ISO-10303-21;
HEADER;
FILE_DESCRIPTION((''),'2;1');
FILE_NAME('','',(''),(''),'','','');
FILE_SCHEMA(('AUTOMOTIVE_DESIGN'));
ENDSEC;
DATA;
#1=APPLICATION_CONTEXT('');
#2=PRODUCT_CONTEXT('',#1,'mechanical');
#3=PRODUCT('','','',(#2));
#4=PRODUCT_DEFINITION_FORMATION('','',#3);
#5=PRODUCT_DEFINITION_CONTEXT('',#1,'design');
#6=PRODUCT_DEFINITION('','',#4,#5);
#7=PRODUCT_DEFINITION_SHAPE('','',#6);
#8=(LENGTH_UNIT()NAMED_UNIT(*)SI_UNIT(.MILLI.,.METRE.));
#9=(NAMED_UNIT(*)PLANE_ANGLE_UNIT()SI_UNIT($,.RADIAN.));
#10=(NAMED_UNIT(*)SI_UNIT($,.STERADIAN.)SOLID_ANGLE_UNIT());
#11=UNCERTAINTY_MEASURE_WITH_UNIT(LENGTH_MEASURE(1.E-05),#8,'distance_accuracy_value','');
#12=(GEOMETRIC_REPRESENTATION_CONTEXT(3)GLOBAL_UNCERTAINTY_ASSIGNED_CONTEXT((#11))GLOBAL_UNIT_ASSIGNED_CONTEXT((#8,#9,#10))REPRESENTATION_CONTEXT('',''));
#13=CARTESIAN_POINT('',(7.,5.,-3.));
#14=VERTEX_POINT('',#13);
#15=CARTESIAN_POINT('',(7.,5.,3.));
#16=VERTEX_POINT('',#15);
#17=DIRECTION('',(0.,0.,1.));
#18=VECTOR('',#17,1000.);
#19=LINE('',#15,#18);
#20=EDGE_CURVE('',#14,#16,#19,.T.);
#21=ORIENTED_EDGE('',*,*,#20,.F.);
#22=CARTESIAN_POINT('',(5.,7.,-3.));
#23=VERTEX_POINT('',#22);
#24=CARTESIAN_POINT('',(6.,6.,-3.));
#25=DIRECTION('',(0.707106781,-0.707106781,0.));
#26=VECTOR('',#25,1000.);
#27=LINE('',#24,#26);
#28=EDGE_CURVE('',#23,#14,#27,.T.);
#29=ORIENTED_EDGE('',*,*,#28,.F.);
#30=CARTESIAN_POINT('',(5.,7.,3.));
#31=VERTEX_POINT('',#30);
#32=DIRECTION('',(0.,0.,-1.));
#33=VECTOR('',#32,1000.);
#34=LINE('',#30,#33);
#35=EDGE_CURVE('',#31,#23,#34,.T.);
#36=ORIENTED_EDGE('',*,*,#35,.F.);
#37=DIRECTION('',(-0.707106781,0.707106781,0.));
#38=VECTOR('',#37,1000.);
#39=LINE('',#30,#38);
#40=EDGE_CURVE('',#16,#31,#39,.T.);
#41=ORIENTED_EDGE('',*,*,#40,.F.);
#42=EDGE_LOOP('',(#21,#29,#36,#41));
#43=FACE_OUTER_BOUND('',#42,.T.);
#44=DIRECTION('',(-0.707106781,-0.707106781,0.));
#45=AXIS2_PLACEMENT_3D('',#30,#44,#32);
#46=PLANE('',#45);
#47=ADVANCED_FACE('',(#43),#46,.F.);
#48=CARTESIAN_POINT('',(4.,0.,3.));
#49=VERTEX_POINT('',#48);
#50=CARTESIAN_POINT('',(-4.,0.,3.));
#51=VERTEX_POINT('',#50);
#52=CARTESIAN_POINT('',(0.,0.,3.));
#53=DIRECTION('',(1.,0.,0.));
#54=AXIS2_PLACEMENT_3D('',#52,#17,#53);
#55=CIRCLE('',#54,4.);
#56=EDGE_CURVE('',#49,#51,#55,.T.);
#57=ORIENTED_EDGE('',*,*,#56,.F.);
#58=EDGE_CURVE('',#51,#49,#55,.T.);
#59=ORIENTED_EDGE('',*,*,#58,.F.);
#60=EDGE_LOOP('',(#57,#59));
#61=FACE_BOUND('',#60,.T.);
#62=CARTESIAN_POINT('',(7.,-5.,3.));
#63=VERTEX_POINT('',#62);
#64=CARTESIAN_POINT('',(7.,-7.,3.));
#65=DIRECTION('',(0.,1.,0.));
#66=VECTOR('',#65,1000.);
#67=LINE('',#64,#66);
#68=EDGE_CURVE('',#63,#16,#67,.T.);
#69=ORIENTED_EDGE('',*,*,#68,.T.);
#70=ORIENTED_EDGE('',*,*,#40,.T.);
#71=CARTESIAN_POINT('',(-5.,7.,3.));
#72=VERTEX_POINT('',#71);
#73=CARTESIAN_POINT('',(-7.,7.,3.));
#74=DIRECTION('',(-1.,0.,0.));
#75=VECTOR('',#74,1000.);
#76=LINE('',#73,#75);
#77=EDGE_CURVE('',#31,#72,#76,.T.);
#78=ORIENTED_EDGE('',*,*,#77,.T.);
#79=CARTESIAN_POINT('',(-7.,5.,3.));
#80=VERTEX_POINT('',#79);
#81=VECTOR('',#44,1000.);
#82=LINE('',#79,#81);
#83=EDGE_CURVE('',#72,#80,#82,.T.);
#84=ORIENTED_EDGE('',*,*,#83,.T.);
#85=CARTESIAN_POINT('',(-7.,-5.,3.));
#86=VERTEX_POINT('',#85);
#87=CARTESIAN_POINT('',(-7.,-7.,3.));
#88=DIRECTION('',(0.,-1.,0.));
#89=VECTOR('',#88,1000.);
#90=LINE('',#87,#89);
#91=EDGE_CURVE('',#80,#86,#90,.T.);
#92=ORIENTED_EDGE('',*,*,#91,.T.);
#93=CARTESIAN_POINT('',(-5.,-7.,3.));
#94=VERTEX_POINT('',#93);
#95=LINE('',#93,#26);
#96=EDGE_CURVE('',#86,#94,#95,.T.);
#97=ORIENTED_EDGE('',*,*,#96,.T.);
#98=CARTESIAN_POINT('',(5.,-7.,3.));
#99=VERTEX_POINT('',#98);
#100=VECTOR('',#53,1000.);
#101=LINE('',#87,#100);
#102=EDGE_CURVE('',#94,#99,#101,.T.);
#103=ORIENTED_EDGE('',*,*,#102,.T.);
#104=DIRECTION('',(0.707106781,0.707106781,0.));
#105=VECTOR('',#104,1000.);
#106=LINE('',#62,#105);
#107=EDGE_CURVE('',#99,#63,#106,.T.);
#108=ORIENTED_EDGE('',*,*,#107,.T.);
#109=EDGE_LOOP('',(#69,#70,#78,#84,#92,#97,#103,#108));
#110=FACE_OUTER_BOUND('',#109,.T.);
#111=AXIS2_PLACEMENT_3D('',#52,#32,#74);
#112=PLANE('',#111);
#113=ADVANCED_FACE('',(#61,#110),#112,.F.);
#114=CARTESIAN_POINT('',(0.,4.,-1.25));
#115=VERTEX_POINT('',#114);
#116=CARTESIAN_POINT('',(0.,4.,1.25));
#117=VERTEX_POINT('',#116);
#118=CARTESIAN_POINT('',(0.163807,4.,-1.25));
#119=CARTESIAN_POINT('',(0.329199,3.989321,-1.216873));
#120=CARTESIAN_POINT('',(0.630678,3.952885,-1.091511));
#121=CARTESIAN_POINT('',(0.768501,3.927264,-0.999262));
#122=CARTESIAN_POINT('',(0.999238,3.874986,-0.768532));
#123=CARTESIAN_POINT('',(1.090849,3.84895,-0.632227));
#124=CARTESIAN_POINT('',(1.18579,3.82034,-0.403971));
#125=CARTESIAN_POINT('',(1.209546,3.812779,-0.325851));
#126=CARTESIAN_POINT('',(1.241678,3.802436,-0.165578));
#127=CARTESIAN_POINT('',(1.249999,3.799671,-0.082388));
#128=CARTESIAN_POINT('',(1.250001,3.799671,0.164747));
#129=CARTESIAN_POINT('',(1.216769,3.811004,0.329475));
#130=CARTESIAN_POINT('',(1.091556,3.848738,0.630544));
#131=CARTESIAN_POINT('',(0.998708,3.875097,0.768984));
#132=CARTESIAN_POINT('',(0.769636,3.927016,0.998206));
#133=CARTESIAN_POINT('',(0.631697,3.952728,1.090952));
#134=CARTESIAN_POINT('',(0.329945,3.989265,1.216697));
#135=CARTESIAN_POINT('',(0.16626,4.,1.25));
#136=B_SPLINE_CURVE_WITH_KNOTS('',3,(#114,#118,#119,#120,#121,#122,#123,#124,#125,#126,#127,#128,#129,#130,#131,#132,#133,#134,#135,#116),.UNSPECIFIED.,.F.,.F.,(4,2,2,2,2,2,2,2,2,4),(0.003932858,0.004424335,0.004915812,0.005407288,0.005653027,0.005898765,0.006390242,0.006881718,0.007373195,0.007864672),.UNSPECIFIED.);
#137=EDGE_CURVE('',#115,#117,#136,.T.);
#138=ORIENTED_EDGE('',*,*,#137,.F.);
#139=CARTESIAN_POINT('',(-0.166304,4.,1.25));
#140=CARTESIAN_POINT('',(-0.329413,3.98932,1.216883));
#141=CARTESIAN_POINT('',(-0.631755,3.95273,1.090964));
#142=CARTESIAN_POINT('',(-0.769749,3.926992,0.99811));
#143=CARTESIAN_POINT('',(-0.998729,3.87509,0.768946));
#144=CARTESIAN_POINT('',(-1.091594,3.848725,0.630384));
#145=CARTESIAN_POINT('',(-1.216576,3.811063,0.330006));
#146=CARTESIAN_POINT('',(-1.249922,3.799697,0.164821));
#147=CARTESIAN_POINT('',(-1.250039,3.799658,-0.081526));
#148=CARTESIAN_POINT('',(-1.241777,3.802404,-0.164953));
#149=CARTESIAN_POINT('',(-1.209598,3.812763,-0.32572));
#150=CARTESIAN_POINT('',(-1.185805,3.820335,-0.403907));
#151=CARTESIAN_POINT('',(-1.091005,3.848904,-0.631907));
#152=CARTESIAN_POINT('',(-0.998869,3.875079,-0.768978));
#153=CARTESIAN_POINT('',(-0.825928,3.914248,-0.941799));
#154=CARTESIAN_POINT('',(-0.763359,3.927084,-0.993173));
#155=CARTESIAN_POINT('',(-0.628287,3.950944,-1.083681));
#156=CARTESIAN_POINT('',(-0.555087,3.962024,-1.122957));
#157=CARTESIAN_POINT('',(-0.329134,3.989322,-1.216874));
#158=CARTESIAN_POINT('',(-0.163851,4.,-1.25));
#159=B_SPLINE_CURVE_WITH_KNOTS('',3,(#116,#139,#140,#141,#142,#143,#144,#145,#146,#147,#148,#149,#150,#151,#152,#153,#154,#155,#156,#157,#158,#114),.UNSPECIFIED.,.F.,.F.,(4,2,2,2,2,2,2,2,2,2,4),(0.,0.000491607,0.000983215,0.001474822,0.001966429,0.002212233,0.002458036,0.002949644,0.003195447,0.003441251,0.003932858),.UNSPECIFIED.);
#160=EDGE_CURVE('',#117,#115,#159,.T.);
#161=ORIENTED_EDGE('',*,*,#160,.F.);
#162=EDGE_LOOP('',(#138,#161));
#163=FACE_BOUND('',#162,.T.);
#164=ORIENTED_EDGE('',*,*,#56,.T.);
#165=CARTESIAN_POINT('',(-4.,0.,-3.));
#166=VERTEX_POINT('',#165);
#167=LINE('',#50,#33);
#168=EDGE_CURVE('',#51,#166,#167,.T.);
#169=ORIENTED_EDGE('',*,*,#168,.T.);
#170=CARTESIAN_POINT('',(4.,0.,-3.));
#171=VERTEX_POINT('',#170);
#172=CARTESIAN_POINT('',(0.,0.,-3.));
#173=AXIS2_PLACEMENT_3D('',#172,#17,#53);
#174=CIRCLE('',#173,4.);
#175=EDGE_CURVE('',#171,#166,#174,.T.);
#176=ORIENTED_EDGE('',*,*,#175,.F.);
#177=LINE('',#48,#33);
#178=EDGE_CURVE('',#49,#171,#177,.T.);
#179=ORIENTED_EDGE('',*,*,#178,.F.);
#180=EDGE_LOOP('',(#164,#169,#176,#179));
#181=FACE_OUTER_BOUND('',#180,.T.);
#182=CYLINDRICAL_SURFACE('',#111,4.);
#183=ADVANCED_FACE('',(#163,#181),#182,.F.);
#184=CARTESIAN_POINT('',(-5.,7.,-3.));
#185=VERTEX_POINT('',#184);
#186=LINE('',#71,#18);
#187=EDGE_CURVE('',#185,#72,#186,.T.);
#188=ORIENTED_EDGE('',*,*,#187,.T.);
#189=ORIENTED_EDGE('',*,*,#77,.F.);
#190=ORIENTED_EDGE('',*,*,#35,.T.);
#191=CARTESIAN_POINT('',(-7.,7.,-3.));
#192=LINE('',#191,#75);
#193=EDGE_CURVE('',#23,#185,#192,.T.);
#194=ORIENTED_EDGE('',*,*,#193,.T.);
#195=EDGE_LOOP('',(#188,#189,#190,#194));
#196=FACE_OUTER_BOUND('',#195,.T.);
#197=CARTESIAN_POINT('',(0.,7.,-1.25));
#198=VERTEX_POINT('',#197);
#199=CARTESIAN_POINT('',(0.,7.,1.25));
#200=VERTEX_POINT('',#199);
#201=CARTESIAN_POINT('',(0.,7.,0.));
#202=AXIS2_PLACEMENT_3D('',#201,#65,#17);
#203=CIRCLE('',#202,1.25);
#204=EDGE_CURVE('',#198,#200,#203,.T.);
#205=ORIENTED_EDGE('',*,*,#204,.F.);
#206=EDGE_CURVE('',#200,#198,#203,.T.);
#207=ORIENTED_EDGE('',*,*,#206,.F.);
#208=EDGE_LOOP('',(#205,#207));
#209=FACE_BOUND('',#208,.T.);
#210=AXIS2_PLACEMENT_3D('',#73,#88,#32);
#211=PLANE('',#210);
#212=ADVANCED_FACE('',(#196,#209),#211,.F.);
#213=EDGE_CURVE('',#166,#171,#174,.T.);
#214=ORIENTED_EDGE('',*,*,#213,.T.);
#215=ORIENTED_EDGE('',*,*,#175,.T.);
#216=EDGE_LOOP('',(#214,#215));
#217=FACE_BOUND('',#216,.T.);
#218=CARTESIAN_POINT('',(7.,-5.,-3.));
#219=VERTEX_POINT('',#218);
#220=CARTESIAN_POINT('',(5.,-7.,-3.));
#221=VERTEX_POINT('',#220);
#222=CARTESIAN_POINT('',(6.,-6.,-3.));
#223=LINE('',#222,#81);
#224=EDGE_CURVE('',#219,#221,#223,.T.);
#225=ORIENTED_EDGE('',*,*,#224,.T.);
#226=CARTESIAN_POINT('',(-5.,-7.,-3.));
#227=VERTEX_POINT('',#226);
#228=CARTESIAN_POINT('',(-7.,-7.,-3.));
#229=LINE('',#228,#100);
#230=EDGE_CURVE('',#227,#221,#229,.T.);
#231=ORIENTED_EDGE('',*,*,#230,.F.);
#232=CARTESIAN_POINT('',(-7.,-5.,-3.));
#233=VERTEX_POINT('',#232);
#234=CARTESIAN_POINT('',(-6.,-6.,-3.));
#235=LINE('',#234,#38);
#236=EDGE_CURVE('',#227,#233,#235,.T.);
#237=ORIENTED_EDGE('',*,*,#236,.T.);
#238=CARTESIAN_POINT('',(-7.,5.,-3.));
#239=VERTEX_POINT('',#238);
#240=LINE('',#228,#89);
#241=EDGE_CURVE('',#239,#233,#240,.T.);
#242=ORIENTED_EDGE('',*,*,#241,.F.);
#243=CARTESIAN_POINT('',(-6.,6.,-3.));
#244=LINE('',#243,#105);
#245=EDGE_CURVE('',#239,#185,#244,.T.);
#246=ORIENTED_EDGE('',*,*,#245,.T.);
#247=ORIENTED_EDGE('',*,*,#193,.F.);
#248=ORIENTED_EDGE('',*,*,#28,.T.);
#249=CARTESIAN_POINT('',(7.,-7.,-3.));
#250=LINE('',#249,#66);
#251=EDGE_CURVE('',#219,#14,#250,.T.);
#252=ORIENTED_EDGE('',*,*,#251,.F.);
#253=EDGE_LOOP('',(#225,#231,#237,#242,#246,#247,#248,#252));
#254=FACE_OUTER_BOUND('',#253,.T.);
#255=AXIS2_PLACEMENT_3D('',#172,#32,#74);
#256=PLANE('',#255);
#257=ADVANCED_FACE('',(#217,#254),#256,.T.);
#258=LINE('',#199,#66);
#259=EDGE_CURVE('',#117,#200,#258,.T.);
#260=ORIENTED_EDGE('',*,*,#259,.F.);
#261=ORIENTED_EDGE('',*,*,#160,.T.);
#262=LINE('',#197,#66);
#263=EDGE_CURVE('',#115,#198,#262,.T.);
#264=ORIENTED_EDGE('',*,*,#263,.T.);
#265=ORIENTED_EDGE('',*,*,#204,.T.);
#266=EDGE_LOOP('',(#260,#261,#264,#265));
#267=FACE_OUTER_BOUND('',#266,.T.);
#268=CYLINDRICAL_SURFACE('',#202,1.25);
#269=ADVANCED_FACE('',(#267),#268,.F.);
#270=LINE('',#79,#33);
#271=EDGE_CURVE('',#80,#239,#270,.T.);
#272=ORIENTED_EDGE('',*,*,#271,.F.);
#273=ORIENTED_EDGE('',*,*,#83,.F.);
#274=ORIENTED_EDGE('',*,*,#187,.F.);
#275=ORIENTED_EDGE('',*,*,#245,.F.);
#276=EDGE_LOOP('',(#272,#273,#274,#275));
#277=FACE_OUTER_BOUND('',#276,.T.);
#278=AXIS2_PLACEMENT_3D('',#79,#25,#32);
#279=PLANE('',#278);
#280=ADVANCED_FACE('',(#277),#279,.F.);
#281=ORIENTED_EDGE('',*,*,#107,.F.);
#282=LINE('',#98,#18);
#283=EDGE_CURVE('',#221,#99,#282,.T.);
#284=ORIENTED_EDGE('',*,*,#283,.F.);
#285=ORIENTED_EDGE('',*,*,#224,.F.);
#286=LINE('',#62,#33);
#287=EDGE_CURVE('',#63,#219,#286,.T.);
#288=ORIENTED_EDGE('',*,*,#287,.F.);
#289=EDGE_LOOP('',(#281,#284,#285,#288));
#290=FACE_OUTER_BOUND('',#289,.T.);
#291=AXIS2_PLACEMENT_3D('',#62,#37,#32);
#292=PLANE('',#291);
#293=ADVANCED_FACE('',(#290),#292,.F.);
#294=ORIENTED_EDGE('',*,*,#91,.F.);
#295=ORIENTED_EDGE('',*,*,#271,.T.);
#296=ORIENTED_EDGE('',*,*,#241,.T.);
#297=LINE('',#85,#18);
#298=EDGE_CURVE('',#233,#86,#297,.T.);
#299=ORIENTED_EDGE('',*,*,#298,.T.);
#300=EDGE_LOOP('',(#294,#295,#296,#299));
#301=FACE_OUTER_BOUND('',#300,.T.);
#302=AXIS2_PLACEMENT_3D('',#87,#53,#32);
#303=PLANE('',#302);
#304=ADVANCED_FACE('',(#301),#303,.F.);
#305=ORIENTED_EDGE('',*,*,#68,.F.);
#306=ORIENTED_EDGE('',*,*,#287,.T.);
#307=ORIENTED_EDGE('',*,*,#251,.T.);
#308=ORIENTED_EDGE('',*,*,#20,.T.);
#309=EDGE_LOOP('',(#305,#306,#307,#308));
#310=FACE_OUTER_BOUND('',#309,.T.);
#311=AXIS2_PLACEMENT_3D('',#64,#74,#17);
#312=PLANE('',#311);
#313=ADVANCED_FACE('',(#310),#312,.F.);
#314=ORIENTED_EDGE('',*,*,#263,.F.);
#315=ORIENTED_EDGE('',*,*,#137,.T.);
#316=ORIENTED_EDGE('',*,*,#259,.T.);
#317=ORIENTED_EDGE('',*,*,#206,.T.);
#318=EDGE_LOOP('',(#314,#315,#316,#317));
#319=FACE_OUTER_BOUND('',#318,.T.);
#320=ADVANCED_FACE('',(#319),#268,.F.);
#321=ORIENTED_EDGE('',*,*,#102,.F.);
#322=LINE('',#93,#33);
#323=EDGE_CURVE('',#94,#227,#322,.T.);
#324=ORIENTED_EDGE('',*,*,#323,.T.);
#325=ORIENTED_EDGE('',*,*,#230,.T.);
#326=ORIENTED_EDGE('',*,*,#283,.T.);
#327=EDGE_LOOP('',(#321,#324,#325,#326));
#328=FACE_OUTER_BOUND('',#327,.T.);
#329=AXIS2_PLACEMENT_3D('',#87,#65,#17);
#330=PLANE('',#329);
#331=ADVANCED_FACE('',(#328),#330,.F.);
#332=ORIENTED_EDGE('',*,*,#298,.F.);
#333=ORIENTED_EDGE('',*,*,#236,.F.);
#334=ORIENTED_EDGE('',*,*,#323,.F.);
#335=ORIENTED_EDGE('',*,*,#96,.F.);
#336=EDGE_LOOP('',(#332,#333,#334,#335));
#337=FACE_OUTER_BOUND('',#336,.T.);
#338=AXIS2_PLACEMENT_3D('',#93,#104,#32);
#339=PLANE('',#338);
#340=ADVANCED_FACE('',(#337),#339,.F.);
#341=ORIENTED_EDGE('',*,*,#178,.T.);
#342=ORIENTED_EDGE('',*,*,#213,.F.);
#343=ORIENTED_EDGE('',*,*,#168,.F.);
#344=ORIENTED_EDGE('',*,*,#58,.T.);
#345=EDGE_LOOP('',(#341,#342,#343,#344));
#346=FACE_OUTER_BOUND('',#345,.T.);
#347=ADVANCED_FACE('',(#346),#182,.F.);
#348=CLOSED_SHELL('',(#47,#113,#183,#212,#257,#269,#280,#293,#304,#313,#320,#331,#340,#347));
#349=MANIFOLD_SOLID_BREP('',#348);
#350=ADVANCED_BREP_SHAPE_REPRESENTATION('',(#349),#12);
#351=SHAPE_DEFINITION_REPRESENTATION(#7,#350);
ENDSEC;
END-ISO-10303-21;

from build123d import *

# Parameters (mm, degrees)
SKETCH_1_W              = 14
SKETCH_1_H              = 14
SKETCH_1_R              = 4
EXTRUDE_1_DEPTH         = 3
HOLE_WIZARD_M3_1_REACH  = 17.937
HOLE_WIZARD_M3_1_BORE_R = 1.25
CHAMFER_2_SIZE          = 2


with BuildPart() as part:
    # 草图1 → 凸台-拉伸1 (new, symmetric)
    with BuildSketch(Plane.XY):
        Rectangle(SKETCH_1_W, SKETCH_1_H)
        Circle(SKETCH_1_R, mode=Mode.SUBTRACT)
    extrude(amount=EXTRUDE_1_DEPTH, both=True)

    # M3 螺纹孔1 bore (on position points) → M3 螺纹孔1 (cut, up to next)
    with BuildSketch(Plane.ZX.offset(7), mode=Mode.PRIVATE) as hole_wizard_m3_1_sk1:
        Circle(HOLE_WIZARD_M3_1_BORE_R)
    hole_wizard_m3_1_tool1 = extrude(hole_wizard_m3_1_sk1.sketch, amount=-HOLE_WIZARD_M3_1_REACH, mode=Mode.PRIVATE) & part.part
    add(hole_wizard_m3_1_tool1.solids().sort_by_distance((0, 7, 0))[0], mode=Mode.SUBTRACT)

    # 倒角2
    chamfer_2_edges = [part.edges().sort_by_distance(p)[0] for p in [
        (7, -7, 0),
        (-7, -7, 0),
        (-7, 7, 0),
        (7, 7, 0),
    ]]
    chamfer(chamfer_2_edges, length=CHAMFER_2_SIZE)


solid = part.part
